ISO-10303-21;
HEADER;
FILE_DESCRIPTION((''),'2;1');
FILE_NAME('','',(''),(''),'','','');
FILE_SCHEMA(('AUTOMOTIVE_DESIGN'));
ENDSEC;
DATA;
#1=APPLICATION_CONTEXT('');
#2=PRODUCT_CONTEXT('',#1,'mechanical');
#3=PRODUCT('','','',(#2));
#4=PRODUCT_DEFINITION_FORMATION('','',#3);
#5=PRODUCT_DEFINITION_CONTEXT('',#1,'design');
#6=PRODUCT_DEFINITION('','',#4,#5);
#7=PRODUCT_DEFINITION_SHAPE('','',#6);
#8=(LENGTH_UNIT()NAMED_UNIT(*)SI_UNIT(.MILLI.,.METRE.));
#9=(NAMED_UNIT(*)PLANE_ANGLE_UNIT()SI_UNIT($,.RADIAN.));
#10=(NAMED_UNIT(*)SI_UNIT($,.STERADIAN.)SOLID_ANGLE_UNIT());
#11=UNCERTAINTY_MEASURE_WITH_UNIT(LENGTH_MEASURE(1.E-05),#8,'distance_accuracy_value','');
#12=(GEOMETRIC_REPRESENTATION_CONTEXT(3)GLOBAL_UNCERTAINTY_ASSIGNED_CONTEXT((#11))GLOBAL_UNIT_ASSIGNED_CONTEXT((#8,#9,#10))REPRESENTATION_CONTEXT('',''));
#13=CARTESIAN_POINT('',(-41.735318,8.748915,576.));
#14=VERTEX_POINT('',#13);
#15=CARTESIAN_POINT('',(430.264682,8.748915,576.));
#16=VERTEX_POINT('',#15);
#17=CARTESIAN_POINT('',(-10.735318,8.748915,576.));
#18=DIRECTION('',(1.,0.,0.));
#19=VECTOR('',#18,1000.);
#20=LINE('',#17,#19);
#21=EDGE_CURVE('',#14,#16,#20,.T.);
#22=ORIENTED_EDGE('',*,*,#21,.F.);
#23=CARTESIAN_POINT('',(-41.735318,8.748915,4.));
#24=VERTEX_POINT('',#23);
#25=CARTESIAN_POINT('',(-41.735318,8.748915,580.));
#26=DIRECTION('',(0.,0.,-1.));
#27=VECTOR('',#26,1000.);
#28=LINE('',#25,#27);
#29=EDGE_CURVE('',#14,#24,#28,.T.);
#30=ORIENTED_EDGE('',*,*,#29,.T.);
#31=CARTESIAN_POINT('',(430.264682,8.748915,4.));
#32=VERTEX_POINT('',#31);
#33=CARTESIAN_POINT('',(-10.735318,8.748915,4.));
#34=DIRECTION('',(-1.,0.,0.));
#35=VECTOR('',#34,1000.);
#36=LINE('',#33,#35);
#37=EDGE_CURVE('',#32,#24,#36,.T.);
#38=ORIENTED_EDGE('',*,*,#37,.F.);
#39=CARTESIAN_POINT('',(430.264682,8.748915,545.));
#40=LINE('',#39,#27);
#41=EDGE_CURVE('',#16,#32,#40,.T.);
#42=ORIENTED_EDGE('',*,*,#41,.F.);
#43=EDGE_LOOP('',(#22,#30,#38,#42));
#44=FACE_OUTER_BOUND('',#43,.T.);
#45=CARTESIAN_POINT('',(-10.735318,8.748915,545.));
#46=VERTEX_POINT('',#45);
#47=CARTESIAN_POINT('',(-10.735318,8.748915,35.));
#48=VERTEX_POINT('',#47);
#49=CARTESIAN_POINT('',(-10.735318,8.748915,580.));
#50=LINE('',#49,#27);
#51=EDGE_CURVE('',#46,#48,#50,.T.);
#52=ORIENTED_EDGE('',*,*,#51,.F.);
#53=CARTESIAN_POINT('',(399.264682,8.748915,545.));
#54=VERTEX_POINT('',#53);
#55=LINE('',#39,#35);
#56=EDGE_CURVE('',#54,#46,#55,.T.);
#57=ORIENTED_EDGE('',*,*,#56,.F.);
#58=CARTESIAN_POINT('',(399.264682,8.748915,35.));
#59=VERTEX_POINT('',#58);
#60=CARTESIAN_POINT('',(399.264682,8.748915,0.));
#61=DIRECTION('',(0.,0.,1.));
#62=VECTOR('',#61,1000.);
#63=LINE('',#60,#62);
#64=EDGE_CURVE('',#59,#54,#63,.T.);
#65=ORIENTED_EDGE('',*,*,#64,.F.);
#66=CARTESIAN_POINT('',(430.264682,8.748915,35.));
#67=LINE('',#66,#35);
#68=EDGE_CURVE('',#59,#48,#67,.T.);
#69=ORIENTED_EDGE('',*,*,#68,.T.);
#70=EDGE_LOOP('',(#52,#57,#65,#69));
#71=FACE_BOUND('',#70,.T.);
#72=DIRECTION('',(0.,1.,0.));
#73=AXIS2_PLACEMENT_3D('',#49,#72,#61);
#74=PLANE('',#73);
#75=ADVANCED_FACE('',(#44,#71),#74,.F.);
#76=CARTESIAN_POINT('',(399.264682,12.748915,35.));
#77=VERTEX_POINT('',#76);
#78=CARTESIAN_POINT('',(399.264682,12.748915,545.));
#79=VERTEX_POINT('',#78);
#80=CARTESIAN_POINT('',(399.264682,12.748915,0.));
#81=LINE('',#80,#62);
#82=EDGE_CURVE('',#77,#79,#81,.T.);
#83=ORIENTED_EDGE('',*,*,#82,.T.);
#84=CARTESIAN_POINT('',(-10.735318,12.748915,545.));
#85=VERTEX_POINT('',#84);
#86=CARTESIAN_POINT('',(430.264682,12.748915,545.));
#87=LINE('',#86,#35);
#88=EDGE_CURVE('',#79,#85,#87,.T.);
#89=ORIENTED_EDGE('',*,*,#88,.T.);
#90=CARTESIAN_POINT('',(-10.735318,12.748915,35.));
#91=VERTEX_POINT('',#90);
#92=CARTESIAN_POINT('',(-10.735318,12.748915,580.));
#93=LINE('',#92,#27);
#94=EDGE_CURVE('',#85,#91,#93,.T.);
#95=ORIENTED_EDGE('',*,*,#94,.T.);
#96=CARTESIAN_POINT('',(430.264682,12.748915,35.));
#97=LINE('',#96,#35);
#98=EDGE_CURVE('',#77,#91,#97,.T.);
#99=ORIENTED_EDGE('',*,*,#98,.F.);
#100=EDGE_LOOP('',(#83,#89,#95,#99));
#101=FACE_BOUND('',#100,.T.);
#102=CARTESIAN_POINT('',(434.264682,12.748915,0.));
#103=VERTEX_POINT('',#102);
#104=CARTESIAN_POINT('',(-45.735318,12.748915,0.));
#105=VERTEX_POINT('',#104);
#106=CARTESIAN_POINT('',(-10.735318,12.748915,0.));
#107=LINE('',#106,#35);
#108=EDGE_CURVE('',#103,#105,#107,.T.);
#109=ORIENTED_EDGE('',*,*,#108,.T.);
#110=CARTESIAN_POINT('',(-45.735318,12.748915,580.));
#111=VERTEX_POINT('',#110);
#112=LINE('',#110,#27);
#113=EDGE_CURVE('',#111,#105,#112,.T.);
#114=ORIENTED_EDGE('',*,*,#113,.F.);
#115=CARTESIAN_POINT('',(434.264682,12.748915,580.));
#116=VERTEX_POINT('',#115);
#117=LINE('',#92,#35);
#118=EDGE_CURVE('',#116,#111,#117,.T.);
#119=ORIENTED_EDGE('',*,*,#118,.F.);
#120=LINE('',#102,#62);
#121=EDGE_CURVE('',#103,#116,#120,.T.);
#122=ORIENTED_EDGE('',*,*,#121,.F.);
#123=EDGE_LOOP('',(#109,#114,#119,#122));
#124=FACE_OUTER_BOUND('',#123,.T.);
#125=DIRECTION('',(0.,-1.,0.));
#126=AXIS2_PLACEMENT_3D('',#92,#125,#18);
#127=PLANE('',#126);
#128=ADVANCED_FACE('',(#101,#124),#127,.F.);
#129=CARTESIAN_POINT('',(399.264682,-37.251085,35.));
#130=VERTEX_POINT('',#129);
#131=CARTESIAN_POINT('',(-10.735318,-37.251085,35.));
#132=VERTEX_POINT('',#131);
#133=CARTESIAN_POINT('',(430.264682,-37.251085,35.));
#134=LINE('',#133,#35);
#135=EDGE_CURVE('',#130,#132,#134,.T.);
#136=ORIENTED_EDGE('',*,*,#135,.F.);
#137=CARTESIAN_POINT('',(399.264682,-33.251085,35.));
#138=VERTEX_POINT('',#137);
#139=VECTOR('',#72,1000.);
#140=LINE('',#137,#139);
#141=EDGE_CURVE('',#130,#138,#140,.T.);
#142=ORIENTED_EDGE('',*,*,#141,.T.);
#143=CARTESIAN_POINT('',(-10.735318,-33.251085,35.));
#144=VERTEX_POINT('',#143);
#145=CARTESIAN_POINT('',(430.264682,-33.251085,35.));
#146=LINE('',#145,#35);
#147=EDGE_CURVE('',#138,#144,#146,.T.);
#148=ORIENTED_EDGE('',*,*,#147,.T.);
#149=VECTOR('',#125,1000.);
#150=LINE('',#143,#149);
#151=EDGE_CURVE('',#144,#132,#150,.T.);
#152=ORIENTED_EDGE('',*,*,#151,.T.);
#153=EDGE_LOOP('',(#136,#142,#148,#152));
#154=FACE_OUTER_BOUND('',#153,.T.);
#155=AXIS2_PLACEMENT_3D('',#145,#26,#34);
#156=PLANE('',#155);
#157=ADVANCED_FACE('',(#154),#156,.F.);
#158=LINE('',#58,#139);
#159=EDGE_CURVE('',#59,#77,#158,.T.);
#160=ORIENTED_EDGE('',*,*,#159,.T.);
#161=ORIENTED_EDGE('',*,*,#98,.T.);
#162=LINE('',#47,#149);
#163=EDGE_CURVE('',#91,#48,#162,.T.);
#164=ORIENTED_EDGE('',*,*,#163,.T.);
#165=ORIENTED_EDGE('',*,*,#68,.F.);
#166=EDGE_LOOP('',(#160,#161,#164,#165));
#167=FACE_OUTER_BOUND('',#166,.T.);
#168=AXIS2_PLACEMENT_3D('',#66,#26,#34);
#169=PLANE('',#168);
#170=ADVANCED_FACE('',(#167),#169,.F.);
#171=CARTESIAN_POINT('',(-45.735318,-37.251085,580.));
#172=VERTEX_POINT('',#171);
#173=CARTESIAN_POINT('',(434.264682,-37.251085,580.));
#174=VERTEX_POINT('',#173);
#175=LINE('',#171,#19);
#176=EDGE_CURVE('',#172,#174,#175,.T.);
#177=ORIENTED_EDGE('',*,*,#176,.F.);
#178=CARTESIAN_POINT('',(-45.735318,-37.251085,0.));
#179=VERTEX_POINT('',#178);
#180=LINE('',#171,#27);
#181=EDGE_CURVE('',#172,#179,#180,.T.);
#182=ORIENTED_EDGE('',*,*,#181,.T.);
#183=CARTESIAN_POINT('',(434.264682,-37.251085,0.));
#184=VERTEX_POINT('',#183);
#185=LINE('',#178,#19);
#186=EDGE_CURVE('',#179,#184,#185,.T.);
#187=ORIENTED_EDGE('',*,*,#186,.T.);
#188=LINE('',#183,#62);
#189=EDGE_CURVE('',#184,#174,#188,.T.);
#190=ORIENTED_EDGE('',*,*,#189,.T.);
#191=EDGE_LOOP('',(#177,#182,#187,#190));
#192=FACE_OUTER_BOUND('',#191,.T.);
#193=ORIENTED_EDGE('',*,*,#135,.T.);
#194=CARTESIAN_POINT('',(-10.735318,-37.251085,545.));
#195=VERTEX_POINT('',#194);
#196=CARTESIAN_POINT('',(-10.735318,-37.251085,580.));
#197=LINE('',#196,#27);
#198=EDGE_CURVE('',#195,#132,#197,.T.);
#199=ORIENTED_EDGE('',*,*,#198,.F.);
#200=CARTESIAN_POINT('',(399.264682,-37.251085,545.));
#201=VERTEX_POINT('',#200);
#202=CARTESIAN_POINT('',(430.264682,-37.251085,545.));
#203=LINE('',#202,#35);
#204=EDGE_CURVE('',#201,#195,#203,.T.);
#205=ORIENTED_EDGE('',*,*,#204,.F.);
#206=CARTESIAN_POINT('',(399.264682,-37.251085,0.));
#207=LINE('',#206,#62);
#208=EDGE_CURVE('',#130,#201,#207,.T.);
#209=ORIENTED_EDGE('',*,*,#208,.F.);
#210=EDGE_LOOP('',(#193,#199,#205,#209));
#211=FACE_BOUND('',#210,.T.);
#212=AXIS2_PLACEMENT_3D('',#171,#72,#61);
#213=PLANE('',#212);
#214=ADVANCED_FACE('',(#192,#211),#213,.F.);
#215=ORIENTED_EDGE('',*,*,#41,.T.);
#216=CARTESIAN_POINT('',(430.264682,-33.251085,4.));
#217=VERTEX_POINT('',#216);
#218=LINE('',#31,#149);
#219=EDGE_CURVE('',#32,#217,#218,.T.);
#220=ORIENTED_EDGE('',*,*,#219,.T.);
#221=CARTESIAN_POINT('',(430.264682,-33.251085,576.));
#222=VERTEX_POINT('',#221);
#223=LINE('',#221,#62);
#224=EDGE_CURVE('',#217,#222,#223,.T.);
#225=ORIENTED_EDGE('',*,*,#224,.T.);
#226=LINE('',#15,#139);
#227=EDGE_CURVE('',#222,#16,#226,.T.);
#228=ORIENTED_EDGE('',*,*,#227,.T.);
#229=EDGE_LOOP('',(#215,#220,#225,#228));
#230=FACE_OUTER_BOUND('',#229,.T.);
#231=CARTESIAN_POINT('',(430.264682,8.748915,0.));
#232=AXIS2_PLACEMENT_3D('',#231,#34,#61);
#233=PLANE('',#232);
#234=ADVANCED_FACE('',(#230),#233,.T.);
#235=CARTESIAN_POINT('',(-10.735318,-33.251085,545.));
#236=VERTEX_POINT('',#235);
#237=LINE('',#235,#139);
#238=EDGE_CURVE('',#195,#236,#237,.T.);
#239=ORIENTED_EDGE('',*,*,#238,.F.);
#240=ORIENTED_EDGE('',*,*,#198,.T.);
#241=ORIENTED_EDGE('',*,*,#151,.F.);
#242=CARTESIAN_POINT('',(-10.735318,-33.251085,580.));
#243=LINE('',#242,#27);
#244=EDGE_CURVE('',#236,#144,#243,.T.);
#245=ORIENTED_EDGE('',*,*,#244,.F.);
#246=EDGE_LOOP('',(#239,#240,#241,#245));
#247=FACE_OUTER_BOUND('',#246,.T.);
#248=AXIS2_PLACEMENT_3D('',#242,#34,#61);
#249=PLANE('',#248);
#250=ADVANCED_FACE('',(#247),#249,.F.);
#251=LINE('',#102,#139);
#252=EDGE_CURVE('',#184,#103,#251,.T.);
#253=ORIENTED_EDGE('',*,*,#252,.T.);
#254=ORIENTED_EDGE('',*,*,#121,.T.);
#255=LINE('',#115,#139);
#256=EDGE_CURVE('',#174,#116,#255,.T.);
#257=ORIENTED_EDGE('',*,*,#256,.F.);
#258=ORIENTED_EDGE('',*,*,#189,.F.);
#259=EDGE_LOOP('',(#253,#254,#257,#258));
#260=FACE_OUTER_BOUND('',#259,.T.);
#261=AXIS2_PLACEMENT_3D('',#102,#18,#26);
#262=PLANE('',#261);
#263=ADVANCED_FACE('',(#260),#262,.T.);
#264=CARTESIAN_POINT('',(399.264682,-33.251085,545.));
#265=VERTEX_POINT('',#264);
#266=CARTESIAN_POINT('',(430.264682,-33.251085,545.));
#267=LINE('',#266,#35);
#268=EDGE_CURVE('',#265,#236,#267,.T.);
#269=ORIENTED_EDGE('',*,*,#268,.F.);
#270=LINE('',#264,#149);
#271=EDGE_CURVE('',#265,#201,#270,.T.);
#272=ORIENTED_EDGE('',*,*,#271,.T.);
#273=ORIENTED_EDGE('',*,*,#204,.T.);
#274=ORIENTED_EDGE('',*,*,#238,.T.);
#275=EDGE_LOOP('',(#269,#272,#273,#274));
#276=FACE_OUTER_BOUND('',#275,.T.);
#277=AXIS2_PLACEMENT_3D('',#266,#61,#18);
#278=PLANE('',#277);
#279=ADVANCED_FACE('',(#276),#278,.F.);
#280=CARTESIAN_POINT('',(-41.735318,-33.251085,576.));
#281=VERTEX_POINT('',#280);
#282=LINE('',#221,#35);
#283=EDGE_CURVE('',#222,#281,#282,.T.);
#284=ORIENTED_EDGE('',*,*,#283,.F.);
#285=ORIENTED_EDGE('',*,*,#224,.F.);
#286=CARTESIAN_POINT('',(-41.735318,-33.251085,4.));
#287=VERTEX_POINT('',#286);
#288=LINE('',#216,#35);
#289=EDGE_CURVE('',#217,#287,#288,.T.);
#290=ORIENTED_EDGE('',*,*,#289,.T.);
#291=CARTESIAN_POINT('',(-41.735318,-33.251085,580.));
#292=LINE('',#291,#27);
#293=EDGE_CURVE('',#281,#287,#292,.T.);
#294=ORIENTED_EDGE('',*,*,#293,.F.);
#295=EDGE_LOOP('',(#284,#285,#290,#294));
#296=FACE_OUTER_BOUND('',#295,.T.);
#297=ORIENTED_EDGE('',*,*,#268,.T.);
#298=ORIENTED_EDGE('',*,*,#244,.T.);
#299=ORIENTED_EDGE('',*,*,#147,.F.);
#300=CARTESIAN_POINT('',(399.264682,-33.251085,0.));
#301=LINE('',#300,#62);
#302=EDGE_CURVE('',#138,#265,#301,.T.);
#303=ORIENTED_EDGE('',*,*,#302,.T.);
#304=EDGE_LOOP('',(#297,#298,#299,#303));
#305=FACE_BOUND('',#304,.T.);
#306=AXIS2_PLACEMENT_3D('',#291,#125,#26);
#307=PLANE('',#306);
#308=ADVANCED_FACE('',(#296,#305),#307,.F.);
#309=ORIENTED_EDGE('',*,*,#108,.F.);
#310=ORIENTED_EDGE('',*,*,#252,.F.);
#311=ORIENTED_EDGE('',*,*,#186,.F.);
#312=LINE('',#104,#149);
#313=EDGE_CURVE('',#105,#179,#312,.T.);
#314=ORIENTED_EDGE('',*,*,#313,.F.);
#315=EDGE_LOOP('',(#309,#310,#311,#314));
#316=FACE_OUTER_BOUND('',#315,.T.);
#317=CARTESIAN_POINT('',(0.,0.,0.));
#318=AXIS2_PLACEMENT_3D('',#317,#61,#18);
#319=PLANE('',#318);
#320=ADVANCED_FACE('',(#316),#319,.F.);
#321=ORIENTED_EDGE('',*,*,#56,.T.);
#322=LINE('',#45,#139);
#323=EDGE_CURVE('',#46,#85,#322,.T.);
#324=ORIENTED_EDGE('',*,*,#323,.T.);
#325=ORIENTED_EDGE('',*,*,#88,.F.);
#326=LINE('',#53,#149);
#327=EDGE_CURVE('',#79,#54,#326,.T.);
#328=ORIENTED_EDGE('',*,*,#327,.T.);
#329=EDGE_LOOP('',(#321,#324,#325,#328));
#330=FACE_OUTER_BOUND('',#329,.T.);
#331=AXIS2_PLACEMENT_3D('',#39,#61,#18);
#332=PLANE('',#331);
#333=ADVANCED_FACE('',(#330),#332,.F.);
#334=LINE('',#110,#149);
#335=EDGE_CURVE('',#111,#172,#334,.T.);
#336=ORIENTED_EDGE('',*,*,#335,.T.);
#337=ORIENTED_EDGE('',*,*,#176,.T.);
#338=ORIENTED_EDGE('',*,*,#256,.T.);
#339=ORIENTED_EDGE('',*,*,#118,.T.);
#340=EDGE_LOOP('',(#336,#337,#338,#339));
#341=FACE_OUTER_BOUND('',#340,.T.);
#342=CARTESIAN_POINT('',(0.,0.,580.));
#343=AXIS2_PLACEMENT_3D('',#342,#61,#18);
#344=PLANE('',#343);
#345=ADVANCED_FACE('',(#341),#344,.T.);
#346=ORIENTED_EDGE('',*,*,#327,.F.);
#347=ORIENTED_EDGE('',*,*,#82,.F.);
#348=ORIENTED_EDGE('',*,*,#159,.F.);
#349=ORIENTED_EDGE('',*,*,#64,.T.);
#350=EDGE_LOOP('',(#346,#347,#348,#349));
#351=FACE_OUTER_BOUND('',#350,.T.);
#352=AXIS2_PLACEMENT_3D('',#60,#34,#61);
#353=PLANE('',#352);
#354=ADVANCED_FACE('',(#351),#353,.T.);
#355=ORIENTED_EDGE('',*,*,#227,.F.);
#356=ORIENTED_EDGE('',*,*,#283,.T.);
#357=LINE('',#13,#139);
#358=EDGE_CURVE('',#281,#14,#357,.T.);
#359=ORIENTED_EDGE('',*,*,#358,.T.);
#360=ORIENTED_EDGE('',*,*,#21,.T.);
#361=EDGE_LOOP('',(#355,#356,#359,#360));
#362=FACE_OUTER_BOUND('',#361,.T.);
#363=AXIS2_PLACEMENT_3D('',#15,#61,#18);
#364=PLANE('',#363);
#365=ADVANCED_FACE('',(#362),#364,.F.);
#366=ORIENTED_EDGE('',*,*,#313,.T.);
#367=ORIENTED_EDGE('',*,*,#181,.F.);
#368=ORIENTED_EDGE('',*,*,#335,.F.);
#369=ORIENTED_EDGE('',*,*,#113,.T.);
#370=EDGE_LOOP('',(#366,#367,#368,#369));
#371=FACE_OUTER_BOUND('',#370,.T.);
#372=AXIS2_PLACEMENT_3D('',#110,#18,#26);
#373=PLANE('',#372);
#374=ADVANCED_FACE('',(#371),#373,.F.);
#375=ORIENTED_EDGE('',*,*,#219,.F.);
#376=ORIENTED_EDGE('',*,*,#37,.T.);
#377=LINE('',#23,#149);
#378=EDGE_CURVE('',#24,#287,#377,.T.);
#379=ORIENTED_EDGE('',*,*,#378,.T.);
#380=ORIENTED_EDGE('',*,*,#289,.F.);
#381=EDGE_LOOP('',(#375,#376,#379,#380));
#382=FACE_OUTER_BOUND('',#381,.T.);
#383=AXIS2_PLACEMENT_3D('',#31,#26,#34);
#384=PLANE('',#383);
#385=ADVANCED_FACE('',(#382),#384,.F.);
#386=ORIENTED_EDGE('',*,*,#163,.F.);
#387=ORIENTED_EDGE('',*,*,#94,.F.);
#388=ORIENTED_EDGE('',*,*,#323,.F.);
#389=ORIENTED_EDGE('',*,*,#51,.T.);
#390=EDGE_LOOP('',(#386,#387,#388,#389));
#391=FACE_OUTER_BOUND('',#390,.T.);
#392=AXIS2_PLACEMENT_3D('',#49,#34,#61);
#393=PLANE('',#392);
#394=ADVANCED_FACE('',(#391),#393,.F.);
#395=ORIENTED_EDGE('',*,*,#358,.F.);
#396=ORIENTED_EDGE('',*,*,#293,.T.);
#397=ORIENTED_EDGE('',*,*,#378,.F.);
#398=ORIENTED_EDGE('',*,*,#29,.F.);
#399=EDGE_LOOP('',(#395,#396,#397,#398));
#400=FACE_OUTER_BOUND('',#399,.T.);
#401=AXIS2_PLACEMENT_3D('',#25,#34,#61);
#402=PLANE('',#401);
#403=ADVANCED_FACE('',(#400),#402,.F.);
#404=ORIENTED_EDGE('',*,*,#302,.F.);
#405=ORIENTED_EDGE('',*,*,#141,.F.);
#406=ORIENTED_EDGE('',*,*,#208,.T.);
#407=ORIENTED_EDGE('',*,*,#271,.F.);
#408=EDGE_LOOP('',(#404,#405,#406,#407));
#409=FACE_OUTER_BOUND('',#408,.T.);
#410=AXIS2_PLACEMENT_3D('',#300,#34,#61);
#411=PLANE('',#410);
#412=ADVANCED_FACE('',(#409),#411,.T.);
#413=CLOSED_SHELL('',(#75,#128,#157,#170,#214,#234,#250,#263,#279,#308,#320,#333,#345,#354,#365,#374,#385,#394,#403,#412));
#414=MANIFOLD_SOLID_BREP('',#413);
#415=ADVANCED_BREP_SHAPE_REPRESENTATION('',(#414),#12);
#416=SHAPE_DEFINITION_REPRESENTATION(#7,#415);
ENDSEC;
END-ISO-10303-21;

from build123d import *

# Parameters (mm, degrees)
BOSS_EXTRUDE1_DEPTH = 580
BOSS_EXTRUDE2_DEPTH = 472
BOSS_EXTRUDE3_DEPTH = 580


with BuildPart() as part:
    # Sketch1 → Boss-Extrude1 (new body)
    with BuildSketch(Plane.XY):
        Polygon((-10.73531847, 12.748914521), (-45.73531847, 12.748914521), (-45.73531847, -37.251085479), (-10.73531847, -37.251085479), (-10.73531847, -33.251085479), (-41.73531847, -33.251085479), (-41.73531847, 8.748914521), (-10.73531847, 8.748914521), align=None)
    extrude(amount=BOSS_EXTRUDE1_DEPTH)

    # Sketch2 → Boss-Extrude2 (add)
    with BuildSketch(Plane(origin=(-41.73531847, 0, 0), x_dir=(0, 0, -1), z_dir=(1, 0, 0))):
        Polygon((-545, 12.748914521), (-580, 12.748914521), (-580, -37.251085479), (-545, -37.251085479), (-545, -33.251085479), (-576, -33.251085479), (-576, 8.748914521), (-545, 8.748914521), align=None)
        Polygon((-35, -33.251085479), (-35, -37.251085479), (0, -37.251085479), (0, 12.748914521), (-35, 12.748914521), (-35, 8.748914521), (-4, 8.748914521), (-4, -33.251085479), align=None)
    extrude(amount=BOSS_EXTRUDE2_DEPTH)

    # Sketch3 → Boss-Extrude3 (add)
    with BuildSketch(Plane.XY.offset(580)):
        Polygon((399.26468153, 12.748914521), (434.26468153, 12.748914521), (434.26468153, -37.251085479), (399.26468153, -37.251085479), (399.26468153, -33.251085479), (430.26468153, -33.251085479), (430.26468153, 8.748914521), (399.26468153, 8.748914521), align=None)
    extrude(amount=-BOSS_EXTRUDE3_DEPTH)


solid = part.part
